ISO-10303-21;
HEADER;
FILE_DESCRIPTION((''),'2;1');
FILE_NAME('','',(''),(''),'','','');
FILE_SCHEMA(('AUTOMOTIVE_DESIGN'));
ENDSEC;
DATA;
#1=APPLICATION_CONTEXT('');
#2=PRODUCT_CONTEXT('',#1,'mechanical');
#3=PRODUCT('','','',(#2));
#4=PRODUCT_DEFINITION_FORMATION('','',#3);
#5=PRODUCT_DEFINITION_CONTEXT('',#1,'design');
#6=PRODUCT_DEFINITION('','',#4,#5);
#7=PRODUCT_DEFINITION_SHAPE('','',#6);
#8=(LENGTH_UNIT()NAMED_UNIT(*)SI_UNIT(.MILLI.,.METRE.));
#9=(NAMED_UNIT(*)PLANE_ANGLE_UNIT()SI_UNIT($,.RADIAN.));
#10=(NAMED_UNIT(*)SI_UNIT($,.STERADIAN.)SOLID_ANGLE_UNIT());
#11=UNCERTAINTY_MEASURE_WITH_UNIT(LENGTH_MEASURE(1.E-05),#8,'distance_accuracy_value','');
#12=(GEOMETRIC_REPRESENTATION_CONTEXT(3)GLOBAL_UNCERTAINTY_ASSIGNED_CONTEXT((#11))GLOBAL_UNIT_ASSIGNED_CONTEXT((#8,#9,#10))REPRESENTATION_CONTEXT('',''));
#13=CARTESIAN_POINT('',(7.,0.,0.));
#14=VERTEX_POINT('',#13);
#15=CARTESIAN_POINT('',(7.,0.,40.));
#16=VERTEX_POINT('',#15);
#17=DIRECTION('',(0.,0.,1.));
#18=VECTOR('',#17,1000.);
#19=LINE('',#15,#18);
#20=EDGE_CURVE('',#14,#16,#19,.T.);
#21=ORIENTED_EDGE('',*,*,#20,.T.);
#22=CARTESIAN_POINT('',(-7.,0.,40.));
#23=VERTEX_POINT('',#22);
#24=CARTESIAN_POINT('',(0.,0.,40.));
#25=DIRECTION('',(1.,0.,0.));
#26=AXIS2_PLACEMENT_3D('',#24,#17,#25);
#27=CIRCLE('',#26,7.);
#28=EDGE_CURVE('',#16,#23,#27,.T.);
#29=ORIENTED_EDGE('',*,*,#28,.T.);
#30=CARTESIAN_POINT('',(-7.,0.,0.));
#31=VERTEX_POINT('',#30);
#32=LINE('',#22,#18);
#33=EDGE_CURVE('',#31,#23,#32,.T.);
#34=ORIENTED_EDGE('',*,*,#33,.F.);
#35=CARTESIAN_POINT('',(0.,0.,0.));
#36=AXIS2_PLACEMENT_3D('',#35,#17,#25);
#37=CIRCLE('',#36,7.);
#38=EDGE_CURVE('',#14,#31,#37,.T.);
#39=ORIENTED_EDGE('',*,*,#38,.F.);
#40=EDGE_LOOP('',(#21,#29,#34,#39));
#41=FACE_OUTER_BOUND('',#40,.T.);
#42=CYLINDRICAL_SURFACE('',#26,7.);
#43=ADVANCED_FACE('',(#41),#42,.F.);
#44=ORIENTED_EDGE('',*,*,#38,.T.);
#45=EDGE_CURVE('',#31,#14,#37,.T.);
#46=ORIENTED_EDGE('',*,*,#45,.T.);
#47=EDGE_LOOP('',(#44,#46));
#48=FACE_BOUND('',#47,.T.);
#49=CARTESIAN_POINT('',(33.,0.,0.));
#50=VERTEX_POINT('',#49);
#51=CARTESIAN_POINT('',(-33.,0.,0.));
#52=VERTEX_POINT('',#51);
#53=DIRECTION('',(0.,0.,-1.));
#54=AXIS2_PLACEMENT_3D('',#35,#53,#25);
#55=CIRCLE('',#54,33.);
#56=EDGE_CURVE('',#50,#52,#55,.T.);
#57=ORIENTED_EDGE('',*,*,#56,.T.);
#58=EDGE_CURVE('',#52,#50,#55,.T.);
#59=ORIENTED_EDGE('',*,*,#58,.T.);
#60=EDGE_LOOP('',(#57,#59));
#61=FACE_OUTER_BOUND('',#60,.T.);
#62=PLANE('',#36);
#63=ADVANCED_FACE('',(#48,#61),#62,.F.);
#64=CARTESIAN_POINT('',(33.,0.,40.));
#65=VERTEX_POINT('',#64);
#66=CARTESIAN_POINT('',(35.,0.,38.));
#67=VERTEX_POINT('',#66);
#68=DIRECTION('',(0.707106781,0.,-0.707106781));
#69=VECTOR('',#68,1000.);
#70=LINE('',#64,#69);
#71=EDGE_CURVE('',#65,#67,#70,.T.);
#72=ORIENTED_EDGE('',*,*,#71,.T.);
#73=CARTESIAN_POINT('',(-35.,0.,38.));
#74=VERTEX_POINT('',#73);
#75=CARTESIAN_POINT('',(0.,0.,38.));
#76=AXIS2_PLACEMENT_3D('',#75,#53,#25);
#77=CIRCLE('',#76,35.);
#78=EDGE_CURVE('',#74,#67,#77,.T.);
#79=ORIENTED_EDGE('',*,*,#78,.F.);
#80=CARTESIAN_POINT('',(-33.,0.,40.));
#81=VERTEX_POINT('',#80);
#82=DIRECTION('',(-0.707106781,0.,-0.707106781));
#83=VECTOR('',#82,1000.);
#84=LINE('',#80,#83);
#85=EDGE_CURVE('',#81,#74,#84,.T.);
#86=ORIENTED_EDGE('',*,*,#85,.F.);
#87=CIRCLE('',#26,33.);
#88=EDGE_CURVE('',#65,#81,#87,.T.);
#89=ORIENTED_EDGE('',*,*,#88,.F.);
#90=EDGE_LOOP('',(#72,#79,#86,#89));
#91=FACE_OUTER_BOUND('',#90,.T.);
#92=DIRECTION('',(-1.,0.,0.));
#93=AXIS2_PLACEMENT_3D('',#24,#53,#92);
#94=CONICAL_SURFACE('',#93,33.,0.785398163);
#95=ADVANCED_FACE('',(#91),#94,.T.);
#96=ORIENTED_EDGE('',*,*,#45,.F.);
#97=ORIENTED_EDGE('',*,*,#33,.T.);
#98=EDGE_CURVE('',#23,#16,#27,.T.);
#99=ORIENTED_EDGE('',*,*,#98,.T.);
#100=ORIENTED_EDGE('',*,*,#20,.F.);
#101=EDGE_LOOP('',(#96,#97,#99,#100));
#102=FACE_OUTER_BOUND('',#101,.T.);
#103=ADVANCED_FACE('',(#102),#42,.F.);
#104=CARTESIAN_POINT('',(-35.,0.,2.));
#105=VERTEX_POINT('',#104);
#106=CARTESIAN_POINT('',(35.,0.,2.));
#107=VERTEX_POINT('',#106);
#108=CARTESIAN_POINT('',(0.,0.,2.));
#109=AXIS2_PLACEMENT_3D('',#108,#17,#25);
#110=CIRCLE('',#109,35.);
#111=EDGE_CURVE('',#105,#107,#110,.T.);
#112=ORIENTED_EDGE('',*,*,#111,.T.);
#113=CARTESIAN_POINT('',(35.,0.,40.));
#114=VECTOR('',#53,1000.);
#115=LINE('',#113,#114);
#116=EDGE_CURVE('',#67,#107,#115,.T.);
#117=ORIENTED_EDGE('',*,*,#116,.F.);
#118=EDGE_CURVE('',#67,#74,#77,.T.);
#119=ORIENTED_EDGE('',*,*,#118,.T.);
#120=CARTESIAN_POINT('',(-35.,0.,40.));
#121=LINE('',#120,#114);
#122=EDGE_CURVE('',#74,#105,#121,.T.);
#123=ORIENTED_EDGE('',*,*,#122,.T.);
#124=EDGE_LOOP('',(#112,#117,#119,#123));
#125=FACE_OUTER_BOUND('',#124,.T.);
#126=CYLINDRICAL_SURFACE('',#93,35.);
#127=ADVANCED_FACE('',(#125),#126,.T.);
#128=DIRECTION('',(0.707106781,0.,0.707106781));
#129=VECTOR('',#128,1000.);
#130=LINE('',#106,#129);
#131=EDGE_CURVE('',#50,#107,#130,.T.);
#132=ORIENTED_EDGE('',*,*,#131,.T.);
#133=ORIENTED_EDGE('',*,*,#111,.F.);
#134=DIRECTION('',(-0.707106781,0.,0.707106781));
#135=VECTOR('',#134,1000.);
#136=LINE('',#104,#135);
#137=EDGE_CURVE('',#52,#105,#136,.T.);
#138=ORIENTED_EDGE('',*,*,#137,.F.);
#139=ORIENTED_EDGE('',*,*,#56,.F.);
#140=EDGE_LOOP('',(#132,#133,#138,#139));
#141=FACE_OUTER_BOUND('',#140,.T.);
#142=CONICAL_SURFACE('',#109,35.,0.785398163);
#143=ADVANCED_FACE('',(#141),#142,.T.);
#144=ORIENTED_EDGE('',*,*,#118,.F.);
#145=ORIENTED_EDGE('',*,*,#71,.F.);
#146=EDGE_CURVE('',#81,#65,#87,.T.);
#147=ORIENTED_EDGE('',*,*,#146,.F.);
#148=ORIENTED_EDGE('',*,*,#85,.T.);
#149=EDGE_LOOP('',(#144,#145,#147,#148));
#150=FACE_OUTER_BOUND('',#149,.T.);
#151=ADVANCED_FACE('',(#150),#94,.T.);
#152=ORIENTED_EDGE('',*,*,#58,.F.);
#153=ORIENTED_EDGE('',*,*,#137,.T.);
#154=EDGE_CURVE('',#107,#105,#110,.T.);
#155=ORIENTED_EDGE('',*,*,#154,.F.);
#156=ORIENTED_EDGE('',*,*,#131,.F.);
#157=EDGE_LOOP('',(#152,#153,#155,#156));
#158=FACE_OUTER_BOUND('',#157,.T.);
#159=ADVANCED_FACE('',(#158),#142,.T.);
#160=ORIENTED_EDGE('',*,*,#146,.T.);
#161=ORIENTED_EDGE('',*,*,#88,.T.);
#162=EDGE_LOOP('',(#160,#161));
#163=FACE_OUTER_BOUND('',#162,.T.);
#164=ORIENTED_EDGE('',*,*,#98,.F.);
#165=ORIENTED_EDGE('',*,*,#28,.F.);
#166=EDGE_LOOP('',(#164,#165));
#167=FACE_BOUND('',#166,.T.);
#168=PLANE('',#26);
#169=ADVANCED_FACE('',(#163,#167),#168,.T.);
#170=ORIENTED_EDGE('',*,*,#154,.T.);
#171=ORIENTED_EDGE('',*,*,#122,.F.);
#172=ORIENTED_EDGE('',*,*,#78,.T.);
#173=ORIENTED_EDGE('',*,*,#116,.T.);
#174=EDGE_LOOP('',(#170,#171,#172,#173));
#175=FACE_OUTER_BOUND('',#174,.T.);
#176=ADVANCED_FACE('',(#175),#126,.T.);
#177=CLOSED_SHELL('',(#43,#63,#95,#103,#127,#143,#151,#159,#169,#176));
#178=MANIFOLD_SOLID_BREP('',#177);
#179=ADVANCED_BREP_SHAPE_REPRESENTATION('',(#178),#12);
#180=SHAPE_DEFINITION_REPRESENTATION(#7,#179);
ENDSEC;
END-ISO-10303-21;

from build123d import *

# Parameters (mm, degrees)
SKETCH1_R           = 35
BOSS_EXTRUDE1_DEPTH = 40
CHAMFER1_SIZE       = 2
M16_TAPPED_HOLE1_D  = 14


with BuildPart() as part:
    # Sketch1 → Boss-Extrude1 (new body)
    with BuildSketch(Plane.XY):
        Circle(SKETCH1_R)
    extrude(amount=BOSS_EXTRUDE1_DEPTH)

    # Chamfer1
    chamfer1_edges = [part.edges().sort_by_distance(p)[0] for p in [
        (-35, 0, 0),
        (-35, 0, 40),
    ]]
    chamfer(chamfer1_edges, length=CHAMFER1_SIZE)

    # M16 Tapped Hole1 (through all)
    with Locations(Plane.XY.offset(40)):
        with Locations((0, 0)):
            Hole(M16_TAPPED_HOLE1_D / 2)


solid = part.part
